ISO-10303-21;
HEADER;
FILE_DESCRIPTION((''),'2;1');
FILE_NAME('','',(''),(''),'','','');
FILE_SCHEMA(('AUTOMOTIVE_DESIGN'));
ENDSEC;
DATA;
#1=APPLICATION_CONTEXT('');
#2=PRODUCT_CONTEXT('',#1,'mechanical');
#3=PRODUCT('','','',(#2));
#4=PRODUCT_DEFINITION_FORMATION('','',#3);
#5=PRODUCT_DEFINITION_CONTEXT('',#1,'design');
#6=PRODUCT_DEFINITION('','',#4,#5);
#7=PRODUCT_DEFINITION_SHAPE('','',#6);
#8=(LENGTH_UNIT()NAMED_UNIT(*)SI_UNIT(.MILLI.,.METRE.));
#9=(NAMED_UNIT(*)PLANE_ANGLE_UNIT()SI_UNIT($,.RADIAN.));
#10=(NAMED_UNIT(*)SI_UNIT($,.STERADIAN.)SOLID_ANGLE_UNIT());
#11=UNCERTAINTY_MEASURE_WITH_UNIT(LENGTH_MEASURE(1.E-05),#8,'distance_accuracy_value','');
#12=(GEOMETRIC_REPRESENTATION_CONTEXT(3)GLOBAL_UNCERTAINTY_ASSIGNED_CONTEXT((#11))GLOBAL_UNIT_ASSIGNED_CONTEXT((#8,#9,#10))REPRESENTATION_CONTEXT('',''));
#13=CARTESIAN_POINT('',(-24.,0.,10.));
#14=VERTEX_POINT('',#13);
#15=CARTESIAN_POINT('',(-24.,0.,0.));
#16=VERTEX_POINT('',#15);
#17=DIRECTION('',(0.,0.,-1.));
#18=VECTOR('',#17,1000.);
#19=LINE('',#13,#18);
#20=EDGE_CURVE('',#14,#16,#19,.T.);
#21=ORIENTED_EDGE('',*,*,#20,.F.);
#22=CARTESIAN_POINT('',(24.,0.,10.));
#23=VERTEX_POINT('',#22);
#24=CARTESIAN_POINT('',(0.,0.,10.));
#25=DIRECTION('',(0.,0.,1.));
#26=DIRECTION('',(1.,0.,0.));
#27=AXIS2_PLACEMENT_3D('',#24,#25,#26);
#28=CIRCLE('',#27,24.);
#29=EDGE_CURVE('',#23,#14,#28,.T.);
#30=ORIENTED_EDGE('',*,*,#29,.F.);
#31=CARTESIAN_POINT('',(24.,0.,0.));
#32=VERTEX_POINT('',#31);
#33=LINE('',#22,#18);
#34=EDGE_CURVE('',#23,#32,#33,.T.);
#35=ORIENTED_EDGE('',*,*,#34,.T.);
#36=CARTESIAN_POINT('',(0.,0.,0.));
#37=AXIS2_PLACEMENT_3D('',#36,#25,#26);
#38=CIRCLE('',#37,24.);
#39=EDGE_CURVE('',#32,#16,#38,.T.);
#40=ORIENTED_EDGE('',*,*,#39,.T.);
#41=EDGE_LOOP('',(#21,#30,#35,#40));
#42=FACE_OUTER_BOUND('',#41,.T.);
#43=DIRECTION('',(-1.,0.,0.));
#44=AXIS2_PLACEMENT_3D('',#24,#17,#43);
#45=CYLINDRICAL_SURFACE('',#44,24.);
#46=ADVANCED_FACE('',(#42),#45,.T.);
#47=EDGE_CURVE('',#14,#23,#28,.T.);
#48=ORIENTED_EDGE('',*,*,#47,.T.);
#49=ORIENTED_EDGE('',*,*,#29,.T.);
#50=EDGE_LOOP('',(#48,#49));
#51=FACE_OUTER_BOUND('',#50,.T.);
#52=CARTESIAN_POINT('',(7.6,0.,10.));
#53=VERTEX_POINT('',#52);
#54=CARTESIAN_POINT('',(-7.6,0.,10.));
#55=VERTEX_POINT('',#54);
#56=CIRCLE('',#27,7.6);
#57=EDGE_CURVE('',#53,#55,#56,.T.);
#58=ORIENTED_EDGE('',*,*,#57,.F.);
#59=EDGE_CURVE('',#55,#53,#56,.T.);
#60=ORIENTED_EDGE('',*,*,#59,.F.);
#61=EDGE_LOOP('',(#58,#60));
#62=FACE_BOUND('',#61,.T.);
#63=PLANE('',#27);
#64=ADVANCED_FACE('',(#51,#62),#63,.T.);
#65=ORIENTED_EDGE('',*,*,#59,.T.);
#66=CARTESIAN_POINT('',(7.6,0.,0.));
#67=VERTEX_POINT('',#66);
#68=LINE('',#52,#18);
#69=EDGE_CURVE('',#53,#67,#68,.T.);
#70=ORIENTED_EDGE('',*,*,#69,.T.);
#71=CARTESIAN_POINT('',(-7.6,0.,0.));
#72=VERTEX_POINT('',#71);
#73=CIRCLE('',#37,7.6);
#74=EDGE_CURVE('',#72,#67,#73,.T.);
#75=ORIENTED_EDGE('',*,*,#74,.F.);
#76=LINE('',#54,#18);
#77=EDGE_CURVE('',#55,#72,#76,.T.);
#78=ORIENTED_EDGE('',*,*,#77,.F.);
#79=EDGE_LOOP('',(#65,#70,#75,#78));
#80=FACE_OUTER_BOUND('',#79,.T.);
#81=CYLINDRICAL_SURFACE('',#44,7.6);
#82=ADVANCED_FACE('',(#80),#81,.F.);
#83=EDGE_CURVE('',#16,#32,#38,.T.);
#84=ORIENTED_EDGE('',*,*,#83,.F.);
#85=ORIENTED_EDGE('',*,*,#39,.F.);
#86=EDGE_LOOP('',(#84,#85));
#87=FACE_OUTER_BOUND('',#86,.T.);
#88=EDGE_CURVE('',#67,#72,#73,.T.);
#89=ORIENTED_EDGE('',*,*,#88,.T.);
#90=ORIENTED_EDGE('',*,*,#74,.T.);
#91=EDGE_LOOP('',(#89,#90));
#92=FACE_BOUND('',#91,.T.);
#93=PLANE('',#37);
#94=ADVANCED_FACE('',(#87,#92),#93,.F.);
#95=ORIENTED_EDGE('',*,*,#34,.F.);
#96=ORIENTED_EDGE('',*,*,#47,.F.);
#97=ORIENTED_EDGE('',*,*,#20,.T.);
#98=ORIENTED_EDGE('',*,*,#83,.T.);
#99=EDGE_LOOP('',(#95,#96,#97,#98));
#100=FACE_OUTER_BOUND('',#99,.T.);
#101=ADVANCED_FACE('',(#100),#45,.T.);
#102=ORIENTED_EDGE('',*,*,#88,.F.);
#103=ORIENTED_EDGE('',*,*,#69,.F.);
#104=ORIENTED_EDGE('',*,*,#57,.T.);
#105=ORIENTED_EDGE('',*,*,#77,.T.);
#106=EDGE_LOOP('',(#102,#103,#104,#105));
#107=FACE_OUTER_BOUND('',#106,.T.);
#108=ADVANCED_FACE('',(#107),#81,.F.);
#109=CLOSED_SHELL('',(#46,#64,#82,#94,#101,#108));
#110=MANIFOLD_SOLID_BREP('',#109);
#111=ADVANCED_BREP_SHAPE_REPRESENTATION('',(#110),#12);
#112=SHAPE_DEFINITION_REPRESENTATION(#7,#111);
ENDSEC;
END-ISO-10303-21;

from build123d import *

# Parameters (mm, degrees)
SKETCH_1_R      = 7.6
EXTRUDE_1_DEPTH = 10


with BuildPart() as part:
    # 草图1 → 凸台-拉伸1 (new body)
    with BuildSketch(Plane.XY):
        with BuildLine():
            ThreePointArc((-23.972773672, -1.142857143), (0, -24), (23.972773672, -1.142857143))
            ThreePointArc((23.972773672, -1.142857143), (0, 24), (-23.972773672, -1.142857143))
        make_face()
        Circle(SKETCH_1_R, mode=Mode.SUBTRACT)
    extrude(amount=EXTRUDE_1_DEPTH)


solid = part.part
